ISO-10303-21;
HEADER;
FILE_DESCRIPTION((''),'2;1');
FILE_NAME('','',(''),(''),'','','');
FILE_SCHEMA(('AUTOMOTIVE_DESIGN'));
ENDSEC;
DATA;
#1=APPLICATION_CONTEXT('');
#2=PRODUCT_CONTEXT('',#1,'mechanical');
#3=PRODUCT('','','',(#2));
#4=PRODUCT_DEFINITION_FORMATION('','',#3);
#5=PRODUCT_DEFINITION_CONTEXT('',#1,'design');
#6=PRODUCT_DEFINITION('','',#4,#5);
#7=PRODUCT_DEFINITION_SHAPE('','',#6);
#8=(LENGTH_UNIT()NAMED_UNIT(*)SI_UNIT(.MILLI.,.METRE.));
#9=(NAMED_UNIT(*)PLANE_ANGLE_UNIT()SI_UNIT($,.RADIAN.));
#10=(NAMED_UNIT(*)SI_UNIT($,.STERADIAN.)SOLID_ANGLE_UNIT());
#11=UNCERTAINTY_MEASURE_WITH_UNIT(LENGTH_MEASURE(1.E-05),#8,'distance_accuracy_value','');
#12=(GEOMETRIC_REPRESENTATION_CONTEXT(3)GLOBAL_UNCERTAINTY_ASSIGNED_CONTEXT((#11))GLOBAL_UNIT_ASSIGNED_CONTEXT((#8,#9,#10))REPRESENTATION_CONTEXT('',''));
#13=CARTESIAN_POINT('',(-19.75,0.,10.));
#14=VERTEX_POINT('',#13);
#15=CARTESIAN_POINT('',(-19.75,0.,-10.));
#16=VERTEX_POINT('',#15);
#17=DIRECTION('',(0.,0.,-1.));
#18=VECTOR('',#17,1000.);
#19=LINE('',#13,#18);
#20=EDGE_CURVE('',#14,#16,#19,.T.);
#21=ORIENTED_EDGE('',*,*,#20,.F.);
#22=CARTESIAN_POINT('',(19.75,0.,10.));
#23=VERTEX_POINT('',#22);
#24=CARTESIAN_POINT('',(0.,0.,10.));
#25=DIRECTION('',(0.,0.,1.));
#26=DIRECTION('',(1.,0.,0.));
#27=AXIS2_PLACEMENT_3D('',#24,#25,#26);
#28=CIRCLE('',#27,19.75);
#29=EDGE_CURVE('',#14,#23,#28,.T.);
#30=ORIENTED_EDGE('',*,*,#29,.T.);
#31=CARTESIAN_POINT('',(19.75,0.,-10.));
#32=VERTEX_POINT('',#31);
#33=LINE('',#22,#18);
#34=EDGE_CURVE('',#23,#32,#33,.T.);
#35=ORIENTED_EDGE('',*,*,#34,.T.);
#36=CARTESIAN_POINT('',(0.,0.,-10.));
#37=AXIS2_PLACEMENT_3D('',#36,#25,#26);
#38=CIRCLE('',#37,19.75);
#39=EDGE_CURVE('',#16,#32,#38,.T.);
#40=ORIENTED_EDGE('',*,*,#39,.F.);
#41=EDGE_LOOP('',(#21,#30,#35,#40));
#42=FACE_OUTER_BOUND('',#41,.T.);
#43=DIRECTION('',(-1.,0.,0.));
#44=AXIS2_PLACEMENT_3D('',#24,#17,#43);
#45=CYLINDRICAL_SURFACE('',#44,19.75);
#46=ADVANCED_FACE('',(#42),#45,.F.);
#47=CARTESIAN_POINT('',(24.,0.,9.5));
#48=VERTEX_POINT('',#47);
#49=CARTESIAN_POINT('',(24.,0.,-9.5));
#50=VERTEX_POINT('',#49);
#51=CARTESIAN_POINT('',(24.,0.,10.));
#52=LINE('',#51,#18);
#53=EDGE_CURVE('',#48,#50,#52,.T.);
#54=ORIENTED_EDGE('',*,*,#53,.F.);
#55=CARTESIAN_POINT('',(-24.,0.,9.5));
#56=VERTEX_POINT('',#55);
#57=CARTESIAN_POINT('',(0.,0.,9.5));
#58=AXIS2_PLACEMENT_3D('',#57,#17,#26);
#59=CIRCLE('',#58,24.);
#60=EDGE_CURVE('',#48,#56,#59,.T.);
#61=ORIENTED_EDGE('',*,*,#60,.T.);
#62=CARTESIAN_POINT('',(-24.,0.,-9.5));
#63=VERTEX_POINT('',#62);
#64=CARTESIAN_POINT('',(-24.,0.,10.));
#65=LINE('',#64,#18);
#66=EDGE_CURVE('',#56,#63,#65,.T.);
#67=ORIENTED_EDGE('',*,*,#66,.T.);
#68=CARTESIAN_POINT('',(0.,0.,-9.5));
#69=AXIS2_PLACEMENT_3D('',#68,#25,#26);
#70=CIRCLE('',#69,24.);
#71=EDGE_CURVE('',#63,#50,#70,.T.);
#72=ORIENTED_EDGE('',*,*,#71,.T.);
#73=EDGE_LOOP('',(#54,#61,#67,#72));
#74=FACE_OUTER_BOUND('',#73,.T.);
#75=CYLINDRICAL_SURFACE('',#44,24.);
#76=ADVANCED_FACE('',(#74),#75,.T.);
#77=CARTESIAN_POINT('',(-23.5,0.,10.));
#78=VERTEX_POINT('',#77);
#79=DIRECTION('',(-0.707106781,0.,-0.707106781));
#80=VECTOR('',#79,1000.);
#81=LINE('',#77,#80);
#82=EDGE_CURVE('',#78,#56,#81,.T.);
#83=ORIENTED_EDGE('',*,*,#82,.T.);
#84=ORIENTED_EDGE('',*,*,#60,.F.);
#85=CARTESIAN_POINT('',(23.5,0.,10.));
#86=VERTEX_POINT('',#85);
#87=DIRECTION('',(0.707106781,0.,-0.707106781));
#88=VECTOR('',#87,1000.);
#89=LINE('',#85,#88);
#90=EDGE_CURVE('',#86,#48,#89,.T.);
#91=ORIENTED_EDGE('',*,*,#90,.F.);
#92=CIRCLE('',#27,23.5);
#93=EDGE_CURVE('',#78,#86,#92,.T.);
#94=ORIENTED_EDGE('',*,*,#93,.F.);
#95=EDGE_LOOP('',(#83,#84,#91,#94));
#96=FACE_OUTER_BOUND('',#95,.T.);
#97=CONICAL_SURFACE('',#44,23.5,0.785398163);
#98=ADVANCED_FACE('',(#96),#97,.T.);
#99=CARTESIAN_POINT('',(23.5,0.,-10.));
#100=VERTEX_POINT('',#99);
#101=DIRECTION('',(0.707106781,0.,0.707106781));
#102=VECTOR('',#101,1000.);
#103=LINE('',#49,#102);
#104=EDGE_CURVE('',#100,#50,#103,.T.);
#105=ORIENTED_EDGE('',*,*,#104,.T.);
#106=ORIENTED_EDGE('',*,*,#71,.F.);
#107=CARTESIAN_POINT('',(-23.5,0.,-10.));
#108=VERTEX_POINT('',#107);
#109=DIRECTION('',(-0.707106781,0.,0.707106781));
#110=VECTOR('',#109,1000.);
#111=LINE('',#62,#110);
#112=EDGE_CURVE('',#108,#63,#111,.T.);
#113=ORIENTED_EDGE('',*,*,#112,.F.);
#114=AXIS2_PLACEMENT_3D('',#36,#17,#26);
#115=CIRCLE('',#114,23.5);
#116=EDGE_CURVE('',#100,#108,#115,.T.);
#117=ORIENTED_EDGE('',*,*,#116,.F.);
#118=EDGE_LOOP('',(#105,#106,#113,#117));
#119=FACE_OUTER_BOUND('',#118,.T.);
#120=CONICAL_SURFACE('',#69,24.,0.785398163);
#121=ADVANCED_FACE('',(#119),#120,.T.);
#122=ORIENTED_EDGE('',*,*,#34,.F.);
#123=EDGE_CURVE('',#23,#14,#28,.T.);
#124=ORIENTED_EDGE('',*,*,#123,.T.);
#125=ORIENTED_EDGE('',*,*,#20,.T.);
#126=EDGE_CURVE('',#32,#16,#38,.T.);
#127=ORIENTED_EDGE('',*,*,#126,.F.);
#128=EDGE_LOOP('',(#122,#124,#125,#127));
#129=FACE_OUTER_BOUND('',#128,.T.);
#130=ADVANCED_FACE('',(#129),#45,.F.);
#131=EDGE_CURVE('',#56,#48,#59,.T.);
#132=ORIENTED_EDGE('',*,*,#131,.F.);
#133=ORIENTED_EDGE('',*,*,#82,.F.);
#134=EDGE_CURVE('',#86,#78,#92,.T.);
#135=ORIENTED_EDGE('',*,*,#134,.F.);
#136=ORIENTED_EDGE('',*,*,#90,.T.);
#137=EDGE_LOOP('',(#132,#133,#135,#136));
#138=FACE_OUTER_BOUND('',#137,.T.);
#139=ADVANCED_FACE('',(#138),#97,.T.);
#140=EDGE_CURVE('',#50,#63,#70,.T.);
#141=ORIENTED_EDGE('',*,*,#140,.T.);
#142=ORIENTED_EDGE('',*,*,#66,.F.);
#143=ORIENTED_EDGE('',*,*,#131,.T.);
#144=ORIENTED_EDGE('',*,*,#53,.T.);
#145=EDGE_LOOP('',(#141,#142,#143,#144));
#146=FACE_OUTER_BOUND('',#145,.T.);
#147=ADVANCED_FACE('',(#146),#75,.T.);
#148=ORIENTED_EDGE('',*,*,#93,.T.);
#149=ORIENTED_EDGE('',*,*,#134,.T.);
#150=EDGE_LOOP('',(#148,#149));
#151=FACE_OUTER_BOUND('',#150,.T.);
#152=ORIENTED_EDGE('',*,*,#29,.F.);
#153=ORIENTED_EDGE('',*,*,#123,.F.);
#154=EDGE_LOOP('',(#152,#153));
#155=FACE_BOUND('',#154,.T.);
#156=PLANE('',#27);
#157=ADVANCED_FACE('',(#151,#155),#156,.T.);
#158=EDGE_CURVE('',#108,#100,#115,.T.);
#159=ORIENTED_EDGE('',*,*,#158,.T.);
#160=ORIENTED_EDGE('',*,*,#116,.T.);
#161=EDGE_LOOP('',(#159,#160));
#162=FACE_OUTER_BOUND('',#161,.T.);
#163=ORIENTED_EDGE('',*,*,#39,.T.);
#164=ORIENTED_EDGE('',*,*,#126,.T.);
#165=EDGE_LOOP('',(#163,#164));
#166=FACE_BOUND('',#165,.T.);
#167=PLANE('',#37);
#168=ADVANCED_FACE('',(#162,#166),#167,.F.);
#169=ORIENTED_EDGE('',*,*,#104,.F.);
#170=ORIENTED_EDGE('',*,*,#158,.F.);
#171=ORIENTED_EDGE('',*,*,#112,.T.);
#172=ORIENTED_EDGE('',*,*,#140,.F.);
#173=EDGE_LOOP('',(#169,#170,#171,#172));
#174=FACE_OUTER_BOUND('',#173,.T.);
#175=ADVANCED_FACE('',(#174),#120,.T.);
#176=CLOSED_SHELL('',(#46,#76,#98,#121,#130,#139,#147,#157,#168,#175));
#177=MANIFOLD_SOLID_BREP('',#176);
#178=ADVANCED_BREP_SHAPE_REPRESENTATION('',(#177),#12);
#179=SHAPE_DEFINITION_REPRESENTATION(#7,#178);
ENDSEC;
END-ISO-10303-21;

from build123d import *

# Parameters (mm, degrees)
SKETCH1_R           = 24
SKETCH1_R_2         = 19.75
BOSS_EXTRUDE1_DEPTH = 10
CHAMFER1_SIZE       = 0.5


with BuildPart() as part:
    # Sketch1 → Boss-Extrude1 (new, symmetric)
    with BuildSketch(Plane.XY):
        Circle(SKETCH1_R)
        Circle(SKETCH1_R_2, mode=Mode.SUBTRACT)
    extrude(amount=BOSS_EXTRUDE1_DEPTH, both=True)

    # Chamfer1
    chamfer1_edges = [part.edges().sort_by_distance(p)[0] for p in [
        (-24, 0, -10),
        (-24, 0, 10),
    ]]
    chamfer(chamfer1_edges, length=CHAMFER1_SIZE)


solid = part.part
